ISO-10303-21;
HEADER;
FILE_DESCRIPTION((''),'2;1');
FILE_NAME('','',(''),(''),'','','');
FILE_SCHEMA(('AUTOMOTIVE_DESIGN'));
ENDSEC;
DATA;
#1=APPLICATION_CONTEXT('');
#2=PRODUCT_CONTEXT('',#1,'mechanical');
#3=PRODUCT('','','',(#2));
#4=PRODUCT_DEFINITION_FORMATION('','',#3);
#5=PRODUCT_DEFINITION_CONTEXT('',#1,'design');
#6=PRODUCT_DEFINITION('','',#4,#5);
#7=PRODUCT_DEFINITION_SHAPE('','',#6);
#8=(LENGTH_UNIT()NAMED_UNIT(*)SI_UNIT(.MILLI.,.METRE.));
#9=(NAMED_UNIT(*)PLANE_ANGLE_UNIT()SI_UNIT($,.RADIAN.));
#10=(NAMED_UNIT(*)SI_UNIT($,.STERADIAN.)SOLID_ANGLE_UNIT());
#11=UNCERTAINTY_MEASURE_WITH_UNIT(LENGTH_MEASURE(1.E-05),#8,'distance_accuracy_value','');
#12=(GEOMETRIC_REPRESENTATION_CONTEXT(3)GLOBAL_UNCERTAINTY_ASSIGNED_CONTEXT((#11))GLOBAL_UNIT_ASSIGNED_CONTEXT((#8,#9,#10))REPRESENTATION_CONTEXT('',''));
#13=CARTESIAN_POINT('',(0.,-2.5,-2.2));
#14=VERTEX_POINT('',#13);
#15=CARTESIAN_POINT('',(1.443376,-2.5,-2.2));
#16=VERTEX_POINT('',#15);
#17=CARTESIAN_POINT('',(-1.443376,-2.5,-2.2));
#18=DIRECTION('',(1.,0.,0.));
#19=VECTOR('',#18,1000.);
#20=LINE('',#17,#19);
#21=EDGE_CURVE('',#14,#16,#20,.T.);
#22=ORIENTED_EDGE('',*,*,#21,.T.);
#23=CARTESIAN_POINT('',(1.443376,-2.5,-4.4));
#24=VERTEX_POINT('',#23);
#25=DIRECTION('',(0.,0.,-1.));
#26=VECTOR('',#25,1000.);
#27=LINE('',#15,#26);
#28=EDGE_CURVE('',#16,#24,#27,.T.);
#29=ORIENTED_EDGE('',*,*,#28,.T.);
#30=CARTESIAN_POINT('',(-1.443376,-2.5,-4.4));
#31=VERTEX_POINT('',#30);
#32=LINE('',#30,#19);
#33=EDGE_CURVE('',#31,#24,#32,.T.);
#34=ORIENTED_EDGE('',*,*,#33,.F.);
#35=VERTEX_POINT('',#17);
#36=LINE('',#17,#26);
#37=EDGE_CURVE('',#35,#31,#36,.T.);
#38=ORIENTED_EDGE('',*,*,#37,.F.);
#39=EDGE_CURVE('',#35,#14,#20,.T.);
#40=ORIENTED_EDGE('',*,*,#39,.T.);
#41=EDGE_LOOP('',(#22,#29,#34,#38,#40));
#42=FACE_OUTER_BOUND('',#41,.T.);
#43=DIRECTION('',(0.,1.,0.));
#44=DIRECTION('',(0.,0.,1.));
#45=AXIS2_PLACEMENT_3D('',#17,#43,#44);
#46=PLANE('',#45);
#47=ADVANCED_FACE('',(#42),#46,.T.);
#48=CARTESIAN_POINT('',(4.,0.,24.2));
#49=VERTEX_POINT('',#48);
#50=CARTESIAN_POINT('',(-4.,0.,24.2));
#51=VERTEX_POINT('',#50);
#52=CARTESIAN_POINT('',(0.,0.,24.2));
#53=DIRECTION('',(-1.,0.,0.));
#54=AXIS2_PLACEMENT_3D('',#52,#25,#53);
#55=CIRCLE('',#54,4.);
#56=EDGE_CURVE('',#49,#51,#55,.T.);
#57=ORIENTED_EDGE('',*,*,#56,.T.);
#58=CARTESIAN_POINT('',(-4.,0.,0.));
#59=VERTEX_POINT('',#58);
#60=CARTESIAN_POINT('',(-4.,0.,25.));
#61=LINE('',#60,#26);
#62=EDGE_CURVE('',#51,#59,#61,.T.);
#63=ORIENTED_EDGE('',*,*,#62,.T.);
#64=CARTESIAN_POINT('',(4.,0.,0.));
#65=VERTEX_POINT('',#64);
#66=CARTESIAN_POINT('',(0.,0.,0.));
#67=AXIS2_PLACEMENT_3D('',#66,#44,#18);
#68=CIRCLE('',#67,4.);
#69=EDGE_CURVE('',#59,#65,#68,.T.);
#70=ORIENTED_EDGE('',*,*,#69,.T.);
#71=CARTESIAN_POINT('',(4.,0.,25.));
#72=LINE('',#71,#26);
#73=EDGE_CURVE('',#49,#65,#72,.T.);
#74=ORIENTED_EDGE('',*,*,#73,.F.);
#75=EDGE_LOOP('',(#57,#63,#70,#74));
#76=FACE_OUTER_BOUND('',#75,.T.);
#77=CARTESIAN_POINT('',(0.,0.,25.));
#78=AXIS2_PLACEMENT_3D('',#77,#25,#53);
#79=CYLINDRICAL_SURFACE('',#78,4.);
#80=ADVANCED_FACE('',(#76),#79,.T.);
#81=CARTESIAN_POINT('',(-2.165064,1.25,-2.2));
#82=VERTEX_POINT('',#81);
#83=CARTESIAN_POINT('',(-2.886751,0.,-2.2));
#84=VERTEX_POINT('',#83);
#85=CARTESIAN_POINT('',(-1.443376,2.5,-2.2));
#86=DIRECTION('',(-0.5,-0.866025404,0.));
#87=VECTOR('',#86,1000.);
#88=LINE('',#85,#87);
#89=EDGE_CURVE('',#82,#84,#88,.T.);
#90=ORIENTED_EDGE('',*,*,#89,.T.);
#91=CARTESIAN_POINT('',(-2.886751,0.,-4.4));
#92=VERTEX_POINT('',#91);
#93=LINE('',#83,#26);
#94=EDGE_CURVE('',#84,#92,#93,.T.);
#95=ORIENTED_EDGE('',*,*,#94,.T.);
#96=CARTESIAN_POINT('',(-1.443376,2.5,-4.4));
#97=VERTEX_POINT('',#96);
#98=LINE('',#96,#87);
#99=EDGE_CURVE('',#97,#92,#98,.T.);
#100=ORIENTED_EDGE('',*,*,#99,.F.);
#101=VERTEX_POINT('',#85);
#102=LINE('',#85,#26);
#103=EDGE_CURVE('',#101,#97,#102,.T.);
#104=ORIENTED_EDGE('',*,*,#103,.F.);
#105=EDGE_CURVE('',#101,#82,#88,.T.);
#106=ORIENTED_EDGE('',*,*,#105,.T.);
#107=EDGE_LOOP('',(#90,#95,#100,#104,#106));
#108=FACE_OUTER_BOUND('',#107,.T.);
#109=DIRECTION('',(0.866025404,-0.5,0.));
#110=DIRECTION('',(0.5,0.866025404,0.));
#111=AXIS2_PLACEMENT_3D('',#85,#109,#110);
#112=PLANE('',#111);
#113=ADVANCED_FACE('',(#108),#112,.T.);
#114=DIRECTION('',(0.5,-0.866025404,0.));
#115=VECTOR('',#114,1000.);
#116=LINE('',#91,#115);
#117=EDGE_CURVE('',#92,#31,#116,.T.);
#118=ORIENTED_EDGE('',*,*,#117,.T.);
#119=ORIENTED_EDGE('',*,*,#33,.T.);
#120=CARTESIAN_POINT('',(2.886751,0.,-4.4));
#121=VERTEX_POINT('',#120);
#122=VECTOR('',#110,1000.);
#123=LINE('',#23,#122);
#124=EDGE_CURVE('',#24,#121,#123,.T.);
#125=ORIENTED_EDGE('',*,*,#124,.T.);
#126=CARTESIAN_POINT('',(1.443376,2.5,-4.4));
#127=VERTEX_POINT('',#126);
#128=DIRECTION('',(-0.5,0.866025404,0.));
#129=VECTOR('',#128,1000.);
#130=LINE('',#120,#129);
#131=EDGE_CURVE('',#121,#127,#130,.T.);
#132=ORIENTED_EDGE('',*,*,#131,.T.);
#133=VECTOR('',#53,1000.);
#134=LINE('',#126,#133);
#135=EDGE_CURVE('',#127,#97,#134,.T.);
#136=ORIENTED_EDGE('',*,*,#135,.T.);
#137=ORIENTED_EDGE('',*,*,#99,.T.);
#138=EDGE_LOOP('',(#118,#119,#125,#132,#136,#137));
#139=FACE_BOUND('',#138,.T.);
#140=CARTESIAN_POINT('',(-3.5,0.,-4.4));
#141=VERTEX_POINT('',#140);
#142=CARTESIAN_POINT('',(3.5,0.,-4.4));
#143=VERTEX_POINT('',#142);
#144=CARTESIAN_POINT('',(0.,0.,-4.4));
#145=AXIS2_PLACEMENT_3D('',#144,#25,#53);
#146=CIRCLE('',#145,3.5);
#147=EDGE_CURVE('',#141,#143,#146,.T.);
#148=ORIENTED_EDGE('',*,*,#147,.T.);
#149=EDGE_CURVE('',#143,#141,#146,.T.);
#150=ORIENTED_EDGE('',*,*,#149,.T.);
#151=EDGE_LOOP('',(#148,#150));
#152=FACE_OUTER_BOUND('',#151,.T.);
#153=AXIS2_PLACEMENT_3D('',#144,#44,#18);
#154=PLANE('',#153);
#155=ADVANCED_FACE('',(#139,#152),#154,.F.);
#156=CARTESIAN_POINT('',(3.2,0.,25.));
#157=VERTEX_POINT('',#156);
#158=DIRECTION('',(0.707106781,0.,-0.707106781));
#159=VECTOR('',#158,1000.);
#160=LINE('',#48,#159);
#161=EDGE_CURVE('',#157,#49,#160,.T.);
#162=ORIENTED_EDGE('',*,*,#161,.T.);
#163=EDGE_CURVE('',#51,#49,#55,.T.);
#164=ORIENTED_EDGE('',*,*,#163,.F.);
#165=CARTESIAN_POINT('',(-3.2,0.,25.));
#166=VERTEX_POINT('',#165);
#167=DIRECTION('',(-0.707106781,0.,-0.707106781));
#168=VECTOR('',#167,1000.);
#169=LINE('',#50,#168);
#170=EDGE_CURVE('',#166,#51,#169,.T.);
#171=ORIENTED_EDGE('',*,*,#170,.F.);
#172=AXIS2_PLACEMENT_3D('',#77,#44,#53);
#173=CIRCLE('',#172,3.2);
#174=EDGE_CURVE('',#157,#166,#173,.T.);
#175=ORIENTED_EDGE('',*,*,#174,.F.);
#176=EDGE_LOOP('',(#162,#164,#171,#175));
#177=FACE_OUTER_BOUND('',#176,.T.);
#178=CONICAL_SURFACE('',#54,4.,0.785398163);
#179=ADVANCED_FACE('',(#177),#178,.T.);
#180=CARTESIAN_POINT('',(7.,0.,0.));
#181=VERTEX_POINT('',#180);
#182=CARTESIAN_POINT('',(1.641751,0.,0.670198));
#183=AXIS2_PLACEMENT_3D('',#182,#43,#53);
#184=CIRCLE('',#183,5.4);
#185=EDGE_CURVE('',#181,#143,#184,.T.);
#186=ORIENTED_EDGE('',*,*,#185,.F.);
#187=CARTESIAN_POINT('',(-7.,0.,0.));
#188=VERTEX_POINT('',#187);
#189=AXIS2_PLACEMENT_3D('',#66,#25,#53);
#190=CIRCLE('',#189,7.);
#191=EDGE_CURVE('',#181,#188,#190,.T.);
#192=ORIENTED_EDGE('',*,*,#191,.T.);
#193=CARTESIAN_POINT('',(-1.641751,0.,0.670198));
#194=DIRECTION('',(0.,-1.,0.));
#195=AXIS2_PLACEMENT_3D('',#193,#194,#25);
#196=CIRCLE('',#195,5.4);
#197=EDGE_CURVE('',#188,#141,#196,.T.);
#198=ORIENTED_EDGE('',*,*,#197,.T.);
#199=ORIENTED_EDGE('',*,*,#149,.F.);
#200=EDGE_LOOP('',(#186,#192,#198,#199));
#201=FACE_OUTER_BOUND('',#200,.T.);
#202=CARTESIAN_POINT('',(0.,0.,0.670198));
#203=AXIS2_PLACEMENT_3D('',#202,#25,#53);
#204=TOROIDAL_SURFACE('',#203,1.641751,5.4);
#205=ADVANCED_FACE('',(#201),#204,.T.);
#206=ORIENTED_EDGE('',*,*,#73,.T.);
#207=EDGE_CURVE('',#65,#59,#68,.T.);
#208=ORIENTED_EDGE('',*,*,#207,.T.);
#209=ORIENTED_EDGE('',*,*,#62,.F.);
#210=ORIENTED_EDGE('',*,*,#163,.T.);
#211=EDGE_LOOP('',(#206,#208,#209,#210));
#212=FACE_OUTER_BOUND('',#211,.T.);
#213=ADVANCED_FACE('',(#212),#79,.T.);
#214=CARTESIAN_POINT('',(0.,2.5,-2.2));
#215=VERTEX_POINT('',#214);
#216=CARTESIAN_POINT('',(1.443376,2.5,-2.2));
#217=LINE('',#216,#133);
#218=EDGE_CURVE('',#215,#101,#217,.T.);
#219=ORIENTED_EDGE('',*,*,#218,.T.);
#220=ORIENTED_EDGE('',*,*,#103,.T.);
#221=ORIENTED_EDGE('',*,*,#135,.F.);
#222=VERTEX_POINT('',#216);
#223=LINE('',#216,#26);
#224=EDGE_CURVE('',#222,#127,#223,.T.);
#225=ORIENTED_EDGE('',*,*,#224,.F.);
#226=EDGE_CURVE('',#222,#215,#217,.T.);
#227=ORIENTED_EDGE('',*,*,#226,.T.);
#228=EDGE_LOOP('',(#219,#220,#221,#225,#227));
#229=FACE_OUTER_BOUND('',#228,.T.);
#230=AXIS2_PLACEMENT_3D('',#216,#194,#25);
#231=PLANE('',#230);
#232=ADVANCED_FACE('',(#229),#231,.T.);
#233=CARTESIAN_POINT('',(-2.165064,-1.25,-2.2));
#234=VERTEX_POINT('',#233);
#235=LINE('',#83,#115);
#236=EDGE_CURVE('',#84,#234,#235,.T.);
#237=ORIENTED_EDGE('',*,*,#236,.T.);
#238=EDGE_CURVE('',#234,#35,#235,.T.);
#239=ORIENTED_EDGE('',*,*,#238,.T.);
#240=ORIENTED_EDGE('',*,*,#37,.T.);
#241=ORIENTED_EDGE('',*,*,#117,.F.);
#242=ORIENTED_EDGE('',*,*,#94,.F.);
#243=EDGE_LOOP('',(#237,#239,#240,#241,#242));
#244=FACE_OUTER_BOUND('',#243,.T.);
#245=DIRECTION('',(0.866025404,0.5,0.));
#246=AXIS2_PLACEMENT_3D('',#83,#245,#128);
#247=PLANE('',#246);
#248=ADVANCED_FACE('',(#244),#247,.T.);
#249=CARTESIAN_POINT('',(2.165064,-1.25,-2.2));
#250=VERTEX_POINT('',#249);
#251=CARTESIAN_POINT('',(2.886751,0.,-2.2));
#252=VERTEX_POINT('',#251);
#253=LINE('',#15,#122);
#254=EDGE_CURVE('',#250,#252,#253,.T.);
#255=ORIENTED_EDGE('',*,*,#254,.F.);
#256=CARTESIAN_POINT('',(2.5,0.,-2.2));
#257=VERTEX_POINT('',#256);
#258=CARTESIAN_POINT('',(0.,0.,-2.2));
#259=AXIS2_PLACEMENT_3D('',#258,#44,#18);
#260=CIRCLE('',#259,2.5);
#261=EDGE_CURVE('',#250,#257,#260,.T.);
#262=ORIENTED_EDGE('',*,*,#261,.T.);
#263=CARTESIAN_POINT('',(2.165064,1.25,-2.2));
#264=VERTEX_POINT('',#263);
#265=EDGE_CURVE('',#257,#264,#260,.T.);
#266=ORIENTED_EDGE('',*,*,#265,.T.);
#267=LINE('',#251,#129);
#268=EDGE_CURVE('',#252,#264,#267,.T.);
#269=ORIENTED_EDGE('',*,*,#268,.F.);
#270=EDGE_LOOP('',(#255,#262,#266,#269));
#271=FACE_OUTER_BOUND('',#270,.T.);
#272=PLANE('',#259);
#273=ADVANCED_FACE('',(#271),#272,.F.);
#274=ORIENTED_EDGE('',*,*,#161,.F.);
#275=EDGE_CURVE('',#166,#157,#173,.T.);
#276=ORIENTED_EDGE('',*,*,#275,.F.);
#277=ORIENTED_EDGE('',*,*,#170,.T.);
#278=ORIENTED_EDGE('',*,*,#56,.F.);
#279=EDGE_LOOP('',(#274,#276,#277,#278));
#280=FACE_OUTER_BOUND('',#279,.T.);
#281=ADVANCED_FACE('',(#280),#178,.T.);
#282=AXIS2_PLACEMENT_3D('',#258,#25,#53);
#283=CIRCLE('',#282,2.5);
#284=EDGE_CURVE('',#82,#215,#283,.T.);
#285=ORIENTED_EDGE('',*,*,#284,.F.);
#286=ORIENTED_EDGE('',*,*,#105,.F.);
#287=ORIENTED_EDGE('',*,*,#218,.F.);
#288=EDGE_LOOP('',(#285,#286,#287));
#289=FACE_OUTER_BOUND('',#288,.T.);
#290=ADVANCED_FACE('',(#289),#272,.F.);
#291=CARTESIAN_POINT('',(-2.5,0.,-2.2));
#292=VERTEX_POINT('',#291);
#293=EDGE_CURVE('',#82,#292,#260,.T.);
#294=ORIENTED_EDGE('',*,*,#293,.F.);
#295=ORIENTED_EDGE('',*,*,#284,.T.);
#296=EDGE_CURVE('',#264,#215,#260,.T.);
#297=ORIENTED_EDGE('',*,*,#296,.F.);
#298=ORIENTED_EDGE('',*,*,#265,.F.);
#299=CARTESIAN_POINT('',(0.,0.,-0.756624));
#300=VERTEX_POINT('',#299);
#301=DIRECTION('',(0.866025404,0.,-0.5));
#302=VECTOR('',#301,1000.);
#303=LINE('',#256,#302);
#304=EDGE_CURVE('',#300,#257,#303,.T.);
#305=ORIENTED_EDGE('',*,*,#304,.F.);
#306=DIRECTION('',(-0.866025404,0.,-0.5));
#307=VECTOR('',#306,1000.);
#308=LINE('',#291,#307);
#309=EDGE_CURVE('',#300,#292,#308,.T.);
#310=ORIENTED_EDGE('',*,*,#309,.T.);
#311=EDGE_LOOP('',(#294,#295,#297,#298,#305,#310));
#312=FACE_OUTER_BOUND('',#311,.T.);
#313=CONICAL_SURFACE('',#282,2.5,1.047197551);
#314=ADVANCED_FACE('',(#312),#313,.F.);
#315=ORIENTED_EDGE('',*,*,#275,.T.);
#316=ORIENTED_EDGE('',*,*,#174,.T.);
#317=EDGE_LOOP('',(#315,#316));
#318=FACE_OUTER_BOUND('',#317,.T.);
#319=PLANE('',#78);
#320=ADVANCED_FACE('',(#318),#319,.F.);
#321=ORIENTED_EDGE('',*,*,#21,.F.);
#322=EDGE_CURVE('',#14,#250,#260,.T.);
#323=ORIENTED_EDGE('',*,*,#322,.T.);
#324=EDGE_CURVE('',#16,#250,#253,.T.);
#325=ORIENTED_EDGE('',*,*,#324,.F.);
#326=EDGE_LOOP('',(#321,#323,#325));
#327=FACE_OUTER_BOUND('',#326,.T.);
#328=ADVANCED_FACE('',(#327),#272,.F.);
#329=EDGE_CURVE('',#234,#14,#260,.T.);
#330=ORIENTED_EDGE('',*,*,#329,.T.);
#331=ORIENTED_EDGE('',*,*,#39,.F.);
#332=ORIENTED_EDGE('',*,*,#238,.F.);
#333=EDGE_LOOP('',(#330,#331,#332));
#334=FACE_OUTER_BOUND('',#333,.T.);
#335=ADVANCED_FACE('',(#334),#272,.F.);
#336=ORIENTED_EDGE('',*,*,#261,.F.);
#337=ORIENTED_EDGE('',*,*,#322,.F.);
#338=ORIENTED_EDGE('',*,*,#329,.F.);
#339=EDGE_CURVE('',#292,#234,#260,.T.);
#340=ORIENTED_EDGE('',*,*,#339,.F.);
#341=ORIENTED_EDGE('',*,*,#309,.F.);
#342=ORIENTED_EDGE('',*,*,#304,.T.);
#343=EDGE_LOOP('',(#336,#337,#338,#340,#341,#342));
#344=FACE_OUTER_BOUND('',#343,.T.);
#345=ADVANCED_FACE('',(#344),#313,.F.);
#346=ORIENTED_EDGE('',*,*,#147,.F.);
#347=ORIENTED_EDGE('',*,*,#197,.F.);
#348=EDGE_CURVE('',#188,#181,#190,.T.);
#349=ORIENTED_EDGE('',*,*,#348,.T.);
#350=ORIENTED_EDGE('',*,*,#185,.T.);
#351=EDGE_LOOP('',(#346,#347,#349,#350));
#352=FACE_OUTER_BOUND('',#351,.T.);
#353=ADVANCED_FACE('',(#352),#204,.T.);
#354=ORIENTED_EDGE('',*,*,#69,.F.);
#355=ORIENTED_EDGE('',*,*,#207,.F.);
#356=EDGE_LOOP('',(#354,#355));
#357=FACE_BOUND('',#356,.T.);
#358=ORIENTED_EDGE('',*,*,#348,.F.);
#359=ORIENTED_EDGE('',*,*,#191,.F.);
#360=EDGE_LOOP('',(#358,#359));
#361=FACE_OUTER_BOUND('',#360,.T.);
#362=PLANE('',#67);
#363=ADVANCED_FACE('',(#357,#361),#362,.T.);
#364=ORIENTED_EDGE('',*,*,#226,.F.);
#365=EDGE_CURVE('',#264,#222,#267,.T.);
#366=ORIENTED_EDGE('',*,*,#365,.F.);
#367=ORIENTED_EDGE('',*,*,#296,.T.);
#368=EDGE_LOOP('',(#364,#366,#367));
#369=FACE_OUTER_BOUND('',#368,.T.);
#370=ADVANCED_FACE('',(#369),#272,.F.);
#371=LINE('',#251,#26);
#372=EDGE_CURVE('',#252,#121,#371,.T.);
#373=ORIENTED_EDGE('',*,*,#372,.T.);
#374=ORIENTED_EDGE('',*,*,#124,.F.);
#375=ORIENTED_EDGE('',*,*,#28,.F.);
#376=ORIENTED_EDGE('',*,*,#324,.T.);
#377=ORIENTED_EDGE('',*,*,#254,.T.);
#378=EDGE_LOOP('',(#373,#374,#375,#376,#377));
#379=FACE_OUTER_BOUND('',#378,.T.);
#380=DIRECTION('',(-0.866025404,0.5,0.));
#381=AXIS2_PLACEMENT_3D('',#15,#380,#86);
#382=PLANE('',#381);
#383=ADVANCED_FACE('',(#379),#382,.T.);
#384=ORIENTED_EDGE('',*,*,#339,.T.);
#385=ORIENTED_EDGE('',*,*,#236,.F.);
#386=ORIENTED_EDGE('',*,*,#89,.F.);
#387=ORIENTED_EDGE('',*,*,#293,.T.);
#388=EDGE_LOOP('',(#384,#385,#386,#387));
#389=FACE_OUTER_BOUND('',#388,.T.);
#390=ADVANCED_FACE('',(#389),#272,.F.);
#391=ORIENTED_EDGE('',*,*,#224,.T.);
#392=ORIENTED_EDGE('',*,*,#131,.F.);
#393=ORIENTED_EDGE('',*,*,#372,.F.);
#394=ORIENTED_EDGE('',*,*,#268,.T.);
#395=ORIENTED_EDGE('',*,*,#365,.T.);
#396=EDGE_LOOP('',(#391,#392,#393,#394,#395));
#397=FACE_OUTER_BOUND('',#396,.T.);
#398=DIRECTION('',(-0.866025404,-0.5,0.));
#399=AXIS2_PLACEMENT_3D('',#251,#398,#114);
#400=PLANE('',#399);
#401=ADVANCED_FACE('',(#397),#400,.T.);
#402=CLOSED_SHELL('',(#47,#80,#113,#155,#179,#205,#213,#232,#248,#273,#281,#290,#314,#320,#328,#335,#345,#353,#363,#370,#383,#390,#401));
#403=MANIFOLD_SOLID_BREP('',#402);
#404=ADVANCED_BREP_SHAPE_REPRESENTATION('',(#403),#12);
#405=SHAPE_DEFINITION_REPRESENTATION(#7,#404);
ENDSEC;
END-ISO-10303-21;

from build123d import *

# Parameters (mm, degrees)
SKETCH_1_R          = 7
EXTRUDE_1_DEPTH     = 4.4
SKETCH_2_R          = 4
EXTRUDE_2_DEPTH     = 25
CHAMFER_1_SIZE      = 0.8
CUT_EXTRUDE_1_DEPTH = 2.2


with BuildPart() as part:
    # 草图1 → 凸台-拉伸1 (new body)
    with BuildSketch(Plane.XY):
        Circle(SKETCH_1_R)
    extrude(amount=-EXTRUDE_1_DEPTH)

    # 草图2 → 凸台-拉伸2 (add)
    with BuildSketch(Plane(origin=(0, 0, 0), x_dir=(-1, 0, 0), z_dir=(0, 0, -1))):
        Circle(SKETCH_2_R)
    extrude(amount=-EXTRUDE_2_DEPTH)

    # 倒角1
    chamfer_1_edges = [part.edges().sort_by_distance(p)[0] for p in [
        (4, 0, 25),
    ]]
    chamfer(chamfer_1_edges, length=CHAMFER_1_SIZE)

    # 草图3 → 切除-拉伸1 (cut)
    with BuildSketch(Plane.XY.offset(-4.4)):
        Polygon((1.443375673, 2.5), (-1.443375673, 2.5), (-2.886751346, 0), (-1.443375673, -2.5), (1.443375673, -2.5), (2.886751346, 0), align=None)
    extrude(amount=CUT_EXTRUDE_1_DEPTH, mode=Mode.SUBTRACT)

    # 草图4 → 切除-旋转1 (revolve, cut)
    with BuildSketch(Plane(origin=(0, 0, 0), x_dir=(0, 1, 0), z_dir=(-1, 0, 0)), mode=Mode.PRIVATE) as cut_revolve_1_sk:
        Polygon((0, 0.756624327), (-2.5, 2.2), (0, 2.2), align=None)
    revolve(cut_revolve_1_sk.sketch.rotate(Axis((0, 0, 0), (0, 0, 1)), 270), axis=Axis((0, 0, 0), (0, 0, 1)), mode=Mode.SUBTRACT)

    # 草图5 → 切除-旋转2 (revolve, cut)
    with BuildSketch(Plane(origin=(0, 0, 0), x_dir=(1, 0, 0), z_dir=(0, 1, 0))):
        with BuildLine():
            Line((-7, 0), (-7, 4.4))
            Line((-7, 4.4), (-3.5, 4.4))
            ThreePointArc((-3.5, 4.4), (-5.867796506, 2.691429039), (-7, 0))
        make_face()
    revolve(axis=Axis((0, 0, 0), (0, 0, 1)), mode=Mode.SUBTRACT)


solid = part.part
